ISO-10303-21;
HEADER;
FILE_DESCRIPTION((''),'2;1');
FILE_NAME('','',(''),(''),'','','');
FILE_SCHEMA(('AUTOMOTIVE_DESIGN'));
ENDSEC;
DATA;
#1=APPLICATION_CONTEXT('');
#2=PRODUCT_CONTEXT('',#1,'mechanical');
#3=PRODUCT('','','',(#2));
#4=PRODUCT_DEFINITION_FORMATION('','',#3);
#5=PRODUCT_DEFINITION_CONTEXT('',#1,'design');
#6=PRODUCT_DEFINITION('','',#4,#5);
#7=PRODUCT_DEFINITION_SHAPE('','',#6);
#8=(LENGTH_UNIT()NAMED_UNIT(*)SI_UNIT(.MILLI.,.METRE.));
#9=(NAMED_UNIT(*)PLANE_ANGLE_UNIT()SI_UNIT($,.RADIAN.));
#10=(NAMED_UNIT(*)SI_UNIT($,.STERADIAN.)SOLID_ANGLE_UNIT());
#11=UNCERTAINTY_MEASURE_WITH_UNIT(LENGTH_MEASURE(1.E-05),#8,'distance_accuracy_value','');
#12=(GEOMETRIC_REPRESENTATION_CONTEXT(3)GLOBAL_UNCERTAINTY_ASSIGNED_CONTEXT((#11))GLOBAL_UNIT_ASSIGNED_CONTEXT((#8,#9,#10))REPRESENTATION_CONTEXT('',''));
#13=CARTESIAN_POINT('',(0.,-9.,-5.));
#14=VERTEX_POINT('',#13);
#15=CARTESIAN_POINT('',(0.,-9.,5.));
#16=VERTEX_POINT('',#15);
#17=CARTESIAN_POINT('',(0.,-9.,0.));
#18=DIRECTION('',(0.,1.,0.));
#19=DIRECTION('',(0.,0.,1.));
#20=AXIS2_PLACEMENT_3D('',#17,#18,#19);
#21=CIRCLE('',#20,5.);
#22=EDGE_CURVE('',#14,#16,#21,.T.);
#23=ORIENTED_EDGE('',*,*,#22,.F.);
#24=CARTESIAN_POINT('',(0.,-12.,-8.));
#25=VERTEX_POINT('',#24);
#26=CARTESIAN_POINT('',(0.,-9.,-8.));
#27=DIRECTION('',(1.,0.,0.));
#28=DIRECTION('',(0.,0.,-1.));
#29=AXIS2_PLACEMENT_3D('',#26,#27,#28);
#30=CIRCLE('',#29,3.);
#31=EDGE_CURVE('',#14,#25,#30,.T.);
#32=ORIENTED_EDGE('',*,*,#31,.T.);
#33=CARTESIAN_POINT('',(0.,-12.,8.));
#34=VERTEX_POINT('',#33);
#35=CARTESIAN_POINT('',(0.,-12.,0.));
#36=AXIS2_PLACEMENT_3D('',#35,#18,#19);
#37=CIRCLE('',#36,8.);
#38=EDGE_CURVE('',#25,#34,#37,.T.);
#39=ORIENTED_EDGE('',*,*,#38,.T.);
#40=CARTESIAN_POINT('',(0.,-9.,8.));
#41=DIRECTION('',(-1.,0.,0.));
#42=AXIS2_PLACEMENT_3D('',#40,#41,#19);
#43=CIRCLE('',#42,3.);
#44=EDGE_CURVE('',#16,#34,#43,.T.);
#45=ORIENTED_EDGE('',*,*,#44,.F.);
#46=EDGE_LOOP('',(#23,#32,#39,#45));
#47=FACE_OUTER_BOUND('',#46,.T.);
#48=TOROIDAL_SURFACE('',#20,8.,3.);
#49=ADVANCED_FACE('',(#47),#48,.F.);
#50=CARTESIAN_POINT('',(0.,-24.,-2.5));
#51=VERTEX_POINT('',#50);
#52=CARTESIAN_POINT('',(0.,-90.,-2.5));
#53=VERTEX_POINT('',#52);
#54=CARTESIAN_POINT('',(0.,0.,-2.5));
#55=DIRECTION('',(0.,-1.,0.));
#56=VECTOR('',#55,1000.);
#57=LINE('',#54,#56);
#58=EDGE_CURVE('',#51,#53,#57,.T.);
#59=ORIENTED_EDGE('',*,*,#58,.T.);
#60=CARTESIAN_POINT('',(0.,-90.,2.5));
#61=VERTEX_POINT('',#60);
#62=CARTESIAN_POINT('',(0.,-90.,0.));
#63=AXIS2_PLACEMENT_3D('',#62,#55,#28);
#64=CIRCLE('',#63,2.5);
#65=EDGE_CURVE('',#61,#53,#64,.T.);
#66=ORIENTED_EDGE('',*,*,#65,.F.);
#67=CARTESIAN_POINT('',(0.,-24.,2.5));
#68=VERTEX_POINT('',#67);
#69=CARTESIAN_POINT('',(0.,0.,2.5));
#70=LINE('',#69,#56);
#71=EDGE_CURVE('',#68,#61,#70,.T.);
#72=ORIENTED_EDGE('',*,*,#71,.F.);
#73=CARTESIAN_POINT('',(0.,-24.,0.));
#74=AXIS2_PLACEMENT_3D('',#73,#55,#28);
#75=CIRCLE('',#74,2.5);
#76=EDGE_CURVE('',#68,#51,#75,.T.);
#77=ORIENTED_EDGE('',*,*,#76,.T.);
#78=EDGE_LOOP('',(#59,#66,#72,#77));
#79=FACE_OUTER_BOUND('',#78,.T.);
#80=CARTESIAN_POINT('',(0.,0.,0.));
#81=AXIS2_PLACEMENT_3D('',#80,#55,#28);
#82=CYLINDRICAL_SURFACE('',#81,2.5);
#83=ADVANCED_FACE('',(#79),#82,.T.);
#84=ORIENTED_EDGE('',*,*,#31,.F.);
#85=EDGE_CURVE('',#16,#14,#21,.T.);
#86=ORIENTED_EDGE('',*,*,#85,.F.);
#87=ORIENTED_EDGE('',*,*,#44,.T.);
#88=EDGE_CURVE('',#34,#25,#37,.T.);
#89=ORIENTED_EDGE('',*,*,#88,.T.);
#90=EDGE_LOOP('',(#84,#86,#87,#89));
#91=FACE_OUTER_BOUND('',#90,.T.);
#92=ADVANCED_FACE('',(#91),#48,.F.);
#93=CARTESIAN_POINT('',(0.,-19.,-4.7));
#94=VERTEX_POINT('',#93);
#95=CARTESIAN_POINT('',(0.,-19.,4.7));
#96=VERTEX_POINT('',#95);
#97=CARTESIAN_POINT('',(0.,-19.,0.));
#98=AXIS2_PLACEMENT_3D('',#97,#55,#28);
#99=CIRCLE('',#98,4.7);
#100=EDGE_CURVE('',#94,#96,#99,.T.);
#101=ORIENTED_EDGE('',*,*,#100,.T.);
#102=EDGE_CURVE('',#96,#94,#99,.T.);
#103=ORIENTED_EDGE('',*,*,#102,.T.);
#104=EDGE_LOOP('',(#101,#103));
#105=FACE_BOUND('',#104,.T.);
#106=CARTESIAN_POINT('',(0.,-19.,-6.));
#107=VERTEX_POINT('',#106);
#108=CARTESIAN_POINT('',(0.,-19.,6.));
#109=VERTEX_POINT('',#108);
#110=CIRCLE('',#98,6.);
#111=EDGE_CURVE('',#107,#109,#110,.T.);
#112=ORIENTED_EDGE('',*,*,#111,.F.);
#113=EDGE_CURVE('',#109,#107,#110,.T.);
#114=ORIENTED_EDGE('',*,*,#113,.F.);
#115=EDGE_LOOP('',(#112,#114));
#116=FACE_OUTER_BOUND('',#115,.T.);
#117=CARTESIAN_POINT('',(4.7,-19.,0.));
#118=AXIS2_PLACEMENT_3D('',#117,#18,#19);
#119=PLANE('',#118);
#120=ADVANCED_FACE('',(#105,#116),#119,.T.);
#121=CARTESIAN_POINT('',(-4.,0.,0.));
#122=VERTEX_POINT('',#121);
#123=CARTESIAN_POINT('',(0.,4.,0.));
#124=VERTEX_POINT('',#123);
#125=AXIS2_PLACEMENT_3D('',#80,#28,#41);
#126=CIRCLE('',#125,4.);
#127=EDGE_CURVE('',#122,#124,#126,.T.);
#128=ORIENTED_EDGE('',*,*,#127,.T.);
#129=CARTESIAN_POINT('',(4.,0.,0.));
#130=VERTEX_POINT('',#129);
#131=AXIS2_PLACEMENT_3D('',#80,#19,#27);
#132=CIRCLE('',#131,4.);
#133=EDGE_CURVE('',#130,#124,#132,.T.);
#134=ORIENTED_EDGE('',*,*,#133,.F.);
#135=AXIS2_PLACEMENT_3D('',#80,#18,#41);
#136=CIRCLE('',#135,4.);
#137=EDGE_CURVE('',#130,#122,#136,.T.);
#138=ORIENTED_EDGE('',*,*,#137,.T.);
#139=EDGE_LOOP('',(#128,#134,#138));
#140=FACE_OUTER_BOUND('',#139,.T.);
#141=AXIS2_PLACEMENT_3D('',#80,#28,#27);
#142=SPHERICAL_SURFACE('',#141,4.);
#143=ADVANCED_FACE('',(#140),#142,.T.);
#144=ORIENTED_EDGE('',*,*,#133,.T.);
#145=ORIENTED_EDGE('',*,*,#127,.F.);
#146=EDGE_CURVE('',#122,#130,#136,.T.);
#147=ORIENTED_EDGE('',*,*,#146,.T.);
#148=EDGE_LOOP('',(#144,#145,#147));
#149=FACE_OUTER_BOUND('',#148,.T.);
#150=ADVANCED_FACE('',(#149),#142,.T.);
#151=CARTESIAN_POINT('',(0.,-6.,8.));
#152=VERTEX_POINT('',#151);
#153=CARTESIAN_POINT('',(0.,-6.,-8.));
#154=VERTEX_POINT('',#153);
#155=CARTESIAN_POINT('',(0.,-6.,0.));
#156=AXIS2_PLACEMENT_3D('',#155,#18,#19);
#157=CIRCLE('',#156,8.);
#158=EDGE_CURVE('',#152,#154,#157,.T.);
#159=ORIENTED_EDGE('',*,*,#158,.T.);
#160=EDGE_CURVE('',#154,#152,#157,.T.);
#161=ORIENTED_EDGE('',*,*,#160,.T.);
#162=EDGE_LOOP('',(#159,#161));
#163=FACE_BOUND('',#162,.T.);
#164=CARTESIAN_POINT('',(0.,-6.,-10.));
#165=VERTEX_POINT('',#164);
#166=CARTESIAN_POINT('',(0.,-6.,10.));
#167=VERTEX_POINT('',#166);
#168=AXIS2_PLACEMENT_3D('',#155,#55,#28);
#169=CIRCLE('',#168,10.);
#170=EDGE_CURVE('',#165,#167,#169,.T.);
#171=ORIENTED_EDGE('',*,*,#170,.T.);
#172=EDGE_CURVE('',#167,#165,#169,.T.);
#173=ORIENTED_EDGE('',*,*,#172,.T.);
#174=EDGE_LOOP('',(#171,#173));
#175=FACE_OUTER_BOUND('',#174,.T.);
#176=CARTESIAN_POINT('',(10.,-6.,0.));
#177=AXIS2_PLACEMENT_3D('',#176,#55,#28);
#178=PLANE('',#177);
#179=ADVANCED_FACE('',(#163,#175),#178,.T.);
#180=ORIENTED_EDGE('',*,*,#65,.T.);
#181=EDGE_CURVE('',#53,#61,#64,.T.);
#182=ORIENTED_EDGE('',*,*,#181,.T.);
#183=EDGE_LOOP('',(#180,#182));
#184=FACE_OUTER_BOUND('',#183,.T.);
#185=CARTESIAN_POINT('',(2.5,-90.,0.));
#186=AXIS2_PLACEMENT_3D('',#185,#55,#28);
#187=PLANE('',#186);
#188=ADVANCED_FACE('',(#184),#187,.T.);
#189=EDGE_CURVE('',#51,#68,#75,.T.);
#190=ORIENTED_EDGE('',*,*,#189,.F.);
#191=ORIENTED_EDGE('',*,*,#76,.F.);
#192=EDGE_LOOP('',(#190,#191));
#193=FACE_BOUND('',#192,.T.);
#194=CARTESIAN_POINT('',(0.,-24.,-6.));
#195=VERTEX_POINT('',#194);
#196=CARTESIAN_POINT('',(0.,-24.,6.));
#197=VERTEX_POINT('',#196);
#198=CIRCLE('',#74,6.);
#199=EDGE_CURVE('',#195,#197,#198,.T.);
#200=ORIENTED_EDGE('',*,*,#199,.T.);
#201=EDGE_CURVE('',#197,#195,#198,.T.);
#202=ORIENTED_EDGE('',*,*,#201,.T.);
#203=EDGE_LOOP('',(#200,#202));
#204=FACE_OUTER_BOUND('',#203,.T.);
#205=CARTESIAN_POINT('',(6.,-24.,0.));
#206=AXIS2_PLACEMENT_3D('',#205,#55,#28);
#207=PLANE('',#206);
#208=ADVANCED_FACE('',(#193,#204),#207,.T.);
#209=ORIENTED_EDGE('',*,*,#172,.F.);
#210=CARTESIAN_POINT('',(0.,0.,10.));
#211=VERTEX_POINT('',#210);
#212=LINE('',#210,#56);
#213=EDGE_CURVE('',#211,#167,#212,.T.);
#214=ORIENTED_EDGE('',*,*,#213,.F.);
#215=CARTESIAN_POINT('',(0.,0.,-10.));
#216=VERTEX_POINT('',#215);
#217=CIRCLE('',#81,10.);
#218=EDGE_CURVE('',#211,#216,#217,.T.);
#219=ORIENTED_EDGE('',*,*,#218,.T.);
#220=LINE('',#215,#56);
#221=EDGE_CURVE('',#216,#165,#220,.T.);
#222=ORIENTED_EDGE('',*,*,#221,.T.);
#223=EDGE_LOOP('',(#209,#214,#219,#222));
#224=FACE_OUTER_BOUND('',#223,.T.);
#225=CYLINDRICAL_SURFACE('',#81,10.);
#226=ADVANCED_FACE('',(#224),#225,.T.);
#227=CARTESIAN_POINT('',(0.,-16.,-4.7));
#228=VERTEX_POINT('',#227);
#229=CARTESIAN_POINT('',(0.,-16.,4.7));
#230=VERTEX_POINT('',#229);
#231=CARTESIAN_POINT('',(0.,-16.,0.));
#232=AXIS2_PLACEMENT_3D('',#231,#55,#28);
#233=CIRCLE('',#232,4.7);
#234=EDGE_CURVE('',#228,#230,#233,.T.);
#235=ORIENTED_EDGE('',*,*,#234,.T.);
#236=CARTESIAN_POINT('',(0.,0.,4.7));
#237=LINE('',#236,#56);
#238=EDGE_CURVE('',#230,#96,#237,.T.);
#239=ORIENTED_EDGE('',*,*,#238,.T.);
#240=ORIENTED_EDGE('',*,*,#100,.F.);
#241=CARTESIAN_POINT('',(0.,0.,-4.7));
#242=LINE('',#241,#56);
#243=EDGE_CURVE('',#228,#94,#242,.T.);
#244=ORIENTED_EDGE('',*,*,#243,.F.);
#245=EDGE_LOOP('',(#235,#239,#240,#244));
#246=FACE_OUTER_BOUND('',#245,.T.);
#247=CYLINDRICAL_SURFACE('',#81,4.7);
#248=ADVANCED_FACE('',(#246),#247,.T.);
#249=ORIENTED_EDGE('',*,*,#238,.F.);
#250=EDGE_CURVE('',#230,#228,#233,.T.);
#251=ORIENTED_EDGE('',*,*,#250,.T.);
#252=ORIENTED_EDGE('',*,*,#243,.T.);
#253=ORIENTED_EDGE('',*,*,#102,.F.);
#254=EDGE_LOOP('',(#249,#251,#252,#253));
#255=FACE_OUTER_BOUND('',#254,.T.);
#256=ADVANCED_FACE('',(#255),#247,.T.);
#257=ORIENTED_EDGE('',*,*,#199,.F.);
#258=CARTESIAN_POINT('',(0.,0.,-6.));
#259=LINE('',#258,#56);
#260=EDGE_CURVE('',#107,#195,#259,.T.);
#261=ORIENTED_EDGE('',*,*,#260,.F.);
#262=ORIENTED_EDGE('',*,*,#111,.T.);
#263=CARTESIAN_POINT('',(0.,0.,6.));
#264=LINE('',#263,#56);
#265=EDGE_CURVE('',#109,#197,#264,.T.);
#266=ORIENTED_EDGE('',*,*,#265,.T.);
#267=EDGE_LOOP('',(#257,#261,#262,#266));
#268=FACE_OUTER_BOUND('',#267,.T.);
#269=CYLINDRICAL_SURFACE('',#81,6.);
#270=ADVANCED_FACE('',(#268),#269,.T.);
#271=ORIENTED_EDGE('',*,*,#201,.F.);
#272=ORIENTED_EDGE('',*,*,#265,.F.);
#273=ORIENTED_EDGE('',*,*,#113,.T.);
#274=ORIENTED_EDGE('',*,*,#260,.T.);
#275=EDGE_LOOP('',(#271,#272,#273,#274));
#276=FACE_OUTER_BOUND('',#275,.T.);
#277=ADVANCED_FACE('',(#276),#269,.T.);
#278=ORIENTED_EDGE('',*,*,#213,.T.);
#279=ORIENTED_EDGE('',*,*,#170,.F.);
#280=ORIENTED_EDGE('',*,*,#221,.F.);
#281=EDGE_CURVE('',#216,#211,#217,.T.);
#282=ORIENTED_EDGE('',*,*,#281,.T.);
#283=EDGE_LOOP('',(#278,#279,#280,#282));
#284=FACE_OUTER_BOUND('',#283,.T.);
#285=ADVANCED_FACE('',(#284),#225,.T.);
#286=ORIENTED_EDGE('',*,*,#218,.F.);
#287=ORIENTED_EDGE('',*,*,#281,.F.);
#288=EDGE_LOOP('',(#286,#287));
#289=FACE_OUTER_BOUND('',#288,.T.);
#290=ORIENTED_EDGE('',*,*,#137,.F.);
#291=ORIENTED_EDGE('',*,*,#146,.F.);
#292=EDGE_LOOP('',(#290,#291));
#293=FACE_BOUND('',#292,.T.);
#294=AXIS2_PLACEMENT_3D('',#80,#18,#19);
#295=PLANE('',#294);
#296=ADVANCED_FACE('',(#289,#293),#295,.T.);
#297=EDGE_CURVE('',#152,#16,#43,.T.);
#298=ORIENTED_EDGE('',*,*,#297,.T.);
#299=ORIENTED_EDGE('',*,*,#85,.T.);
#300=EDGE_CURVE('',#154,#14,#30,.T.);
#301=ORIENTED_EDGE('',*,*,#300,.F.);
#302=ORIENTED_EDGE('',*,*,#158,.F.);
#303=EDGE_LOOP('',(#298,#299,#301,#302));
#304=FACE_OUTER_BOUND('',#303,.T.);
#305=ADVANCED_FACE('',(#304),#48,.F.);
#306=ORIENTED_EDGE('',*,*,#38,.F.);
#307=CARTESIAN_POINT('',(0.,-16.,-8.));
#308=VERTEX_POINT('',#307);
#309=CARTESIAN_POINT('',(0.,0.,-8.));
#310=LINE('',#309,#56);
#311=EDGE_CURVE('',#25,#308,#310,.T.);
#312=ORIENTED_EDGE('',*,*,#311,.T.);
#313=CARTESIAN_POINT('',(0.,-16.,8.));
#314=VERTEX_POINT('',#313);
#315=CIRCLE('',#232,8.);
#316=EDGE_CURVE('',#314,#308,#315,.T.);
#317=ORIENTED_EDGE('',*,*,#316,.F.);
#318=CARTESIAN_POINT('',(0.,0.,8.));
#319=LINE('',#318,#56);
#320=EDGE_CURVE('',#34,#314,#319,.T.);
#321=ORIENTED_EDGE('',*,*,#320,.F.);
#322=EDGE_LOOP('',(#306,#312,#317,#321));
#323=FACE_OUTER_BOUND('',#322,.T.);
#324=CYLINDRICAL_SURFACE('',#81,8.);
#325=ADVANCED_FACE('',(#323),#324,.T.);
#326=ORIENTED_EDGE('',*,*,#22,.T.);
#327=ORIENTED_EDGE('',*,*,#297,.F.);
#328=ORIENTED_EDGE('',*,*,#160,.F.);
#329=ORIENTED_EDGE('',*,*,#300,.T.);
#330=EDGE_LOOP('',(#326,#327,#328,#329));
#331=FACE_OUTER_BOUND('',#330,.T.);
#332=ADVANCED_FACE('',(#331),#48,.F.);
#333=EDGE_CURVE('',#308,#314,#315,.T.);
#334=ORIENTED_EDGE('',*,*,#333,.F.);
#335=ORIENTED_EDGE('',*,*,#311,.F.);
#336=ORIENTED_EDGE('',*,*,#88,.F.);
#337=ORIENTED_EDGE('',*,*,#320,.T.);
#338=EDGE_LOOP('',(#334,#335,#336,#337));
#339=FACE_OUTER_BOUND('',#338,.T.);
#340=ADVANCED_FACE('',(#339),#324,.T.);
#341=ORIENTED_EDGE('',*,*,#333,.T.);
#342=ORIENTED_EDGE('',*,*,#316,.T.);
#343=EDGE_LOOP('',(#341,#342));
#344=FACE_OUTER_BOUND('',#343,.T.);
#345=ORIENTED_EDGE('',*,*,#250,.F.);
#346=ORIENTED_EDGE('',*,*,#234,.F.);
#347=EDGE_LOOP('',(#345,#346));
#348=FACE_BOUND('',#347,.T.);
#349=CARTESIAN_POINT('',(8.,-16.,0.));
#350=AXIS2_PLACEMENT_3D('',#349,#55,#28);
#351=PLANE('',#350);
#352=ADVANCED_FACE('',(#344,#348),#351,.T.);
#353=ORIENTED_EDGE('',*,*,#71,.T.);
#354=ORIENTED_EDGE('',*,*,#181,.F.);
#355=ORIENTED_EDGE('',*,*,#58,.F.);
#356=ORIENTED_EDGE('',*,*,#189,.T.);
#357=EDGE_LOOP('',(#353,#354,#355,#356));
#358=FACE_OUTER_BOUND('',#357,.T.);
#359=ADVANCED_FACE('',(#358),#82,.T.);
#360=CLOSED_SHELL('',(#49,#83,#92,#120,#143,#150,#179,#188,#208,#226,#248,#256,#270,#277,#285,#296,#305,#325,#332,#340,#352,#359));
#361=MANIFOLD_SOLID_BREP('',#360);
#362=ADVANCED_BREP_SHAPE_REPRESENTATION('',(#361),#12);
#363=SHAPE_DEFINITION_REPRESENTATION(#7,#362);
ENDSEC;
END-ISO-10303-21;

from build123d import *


with BuildPart() as part:
    # Sketch1 → Revolve1 (revolve)
    with BuildSketch(Plane.XY, mode=Mode.PRIVATE) as revolve1_sk:
        Polygon((0, 0), (10, 0), (10, -6), (8, -6), (8, -16), (4.7, -16), (4.7, -19), (6, -19), (6, -24), (2.5, -24), (2.5, -90), (0, -90), align=None)
    revolve(revolve1_sk.sketch.rotate(Axis((0, 0, 0), (0, 1, 0)), 90), axis=Axis((0, 0, 0), (0, 1, 0)))

    # Sketch2 → Cut-Revolve1 (revolve, cut)
    with BuildSketch(Plane.XY, mode=Mode.PRIVATE) as cut_revolve1_sk:
        with BuildLine():
            Line((8, -6), (17.813862568, -6))
            Line((17.813862568, -6), (17.813862568, -12))
            Line((17.813862568, -12), (8, -12))
            ThreePointArc((8, -12), (5, -9), (8, -6))
        make_face()
    revolve(cut_revolve1_sk.sketch.rotate(Axis((0, 5.105729486, 0), (0, -1, 0)), 270), axis=Axis((0, 5.105729486, 0), (0, -1, 0)), mode=Mode.SUBTRACT)

    # Sketch4 → Revolve3 (revolve)
    with BuildSketch(Plane.XY, mode=Mode.PRIVATE) as revolve3_sk:
        with BuildLine():
            Line((0, 4), (0, 0))
            Line((0, 0), (4, 0))
            ThreePointArc((4, 0), (2.828427125, 2.828427125), (0, 4))
        make_face()
    revolve(revolve3_sk.sketch.rotate(Axis((0, 4, 0), (0, -1, 0)), 90), axis=Axis((0, 4, 0), (0, -1, 0)))


solid = part.part
